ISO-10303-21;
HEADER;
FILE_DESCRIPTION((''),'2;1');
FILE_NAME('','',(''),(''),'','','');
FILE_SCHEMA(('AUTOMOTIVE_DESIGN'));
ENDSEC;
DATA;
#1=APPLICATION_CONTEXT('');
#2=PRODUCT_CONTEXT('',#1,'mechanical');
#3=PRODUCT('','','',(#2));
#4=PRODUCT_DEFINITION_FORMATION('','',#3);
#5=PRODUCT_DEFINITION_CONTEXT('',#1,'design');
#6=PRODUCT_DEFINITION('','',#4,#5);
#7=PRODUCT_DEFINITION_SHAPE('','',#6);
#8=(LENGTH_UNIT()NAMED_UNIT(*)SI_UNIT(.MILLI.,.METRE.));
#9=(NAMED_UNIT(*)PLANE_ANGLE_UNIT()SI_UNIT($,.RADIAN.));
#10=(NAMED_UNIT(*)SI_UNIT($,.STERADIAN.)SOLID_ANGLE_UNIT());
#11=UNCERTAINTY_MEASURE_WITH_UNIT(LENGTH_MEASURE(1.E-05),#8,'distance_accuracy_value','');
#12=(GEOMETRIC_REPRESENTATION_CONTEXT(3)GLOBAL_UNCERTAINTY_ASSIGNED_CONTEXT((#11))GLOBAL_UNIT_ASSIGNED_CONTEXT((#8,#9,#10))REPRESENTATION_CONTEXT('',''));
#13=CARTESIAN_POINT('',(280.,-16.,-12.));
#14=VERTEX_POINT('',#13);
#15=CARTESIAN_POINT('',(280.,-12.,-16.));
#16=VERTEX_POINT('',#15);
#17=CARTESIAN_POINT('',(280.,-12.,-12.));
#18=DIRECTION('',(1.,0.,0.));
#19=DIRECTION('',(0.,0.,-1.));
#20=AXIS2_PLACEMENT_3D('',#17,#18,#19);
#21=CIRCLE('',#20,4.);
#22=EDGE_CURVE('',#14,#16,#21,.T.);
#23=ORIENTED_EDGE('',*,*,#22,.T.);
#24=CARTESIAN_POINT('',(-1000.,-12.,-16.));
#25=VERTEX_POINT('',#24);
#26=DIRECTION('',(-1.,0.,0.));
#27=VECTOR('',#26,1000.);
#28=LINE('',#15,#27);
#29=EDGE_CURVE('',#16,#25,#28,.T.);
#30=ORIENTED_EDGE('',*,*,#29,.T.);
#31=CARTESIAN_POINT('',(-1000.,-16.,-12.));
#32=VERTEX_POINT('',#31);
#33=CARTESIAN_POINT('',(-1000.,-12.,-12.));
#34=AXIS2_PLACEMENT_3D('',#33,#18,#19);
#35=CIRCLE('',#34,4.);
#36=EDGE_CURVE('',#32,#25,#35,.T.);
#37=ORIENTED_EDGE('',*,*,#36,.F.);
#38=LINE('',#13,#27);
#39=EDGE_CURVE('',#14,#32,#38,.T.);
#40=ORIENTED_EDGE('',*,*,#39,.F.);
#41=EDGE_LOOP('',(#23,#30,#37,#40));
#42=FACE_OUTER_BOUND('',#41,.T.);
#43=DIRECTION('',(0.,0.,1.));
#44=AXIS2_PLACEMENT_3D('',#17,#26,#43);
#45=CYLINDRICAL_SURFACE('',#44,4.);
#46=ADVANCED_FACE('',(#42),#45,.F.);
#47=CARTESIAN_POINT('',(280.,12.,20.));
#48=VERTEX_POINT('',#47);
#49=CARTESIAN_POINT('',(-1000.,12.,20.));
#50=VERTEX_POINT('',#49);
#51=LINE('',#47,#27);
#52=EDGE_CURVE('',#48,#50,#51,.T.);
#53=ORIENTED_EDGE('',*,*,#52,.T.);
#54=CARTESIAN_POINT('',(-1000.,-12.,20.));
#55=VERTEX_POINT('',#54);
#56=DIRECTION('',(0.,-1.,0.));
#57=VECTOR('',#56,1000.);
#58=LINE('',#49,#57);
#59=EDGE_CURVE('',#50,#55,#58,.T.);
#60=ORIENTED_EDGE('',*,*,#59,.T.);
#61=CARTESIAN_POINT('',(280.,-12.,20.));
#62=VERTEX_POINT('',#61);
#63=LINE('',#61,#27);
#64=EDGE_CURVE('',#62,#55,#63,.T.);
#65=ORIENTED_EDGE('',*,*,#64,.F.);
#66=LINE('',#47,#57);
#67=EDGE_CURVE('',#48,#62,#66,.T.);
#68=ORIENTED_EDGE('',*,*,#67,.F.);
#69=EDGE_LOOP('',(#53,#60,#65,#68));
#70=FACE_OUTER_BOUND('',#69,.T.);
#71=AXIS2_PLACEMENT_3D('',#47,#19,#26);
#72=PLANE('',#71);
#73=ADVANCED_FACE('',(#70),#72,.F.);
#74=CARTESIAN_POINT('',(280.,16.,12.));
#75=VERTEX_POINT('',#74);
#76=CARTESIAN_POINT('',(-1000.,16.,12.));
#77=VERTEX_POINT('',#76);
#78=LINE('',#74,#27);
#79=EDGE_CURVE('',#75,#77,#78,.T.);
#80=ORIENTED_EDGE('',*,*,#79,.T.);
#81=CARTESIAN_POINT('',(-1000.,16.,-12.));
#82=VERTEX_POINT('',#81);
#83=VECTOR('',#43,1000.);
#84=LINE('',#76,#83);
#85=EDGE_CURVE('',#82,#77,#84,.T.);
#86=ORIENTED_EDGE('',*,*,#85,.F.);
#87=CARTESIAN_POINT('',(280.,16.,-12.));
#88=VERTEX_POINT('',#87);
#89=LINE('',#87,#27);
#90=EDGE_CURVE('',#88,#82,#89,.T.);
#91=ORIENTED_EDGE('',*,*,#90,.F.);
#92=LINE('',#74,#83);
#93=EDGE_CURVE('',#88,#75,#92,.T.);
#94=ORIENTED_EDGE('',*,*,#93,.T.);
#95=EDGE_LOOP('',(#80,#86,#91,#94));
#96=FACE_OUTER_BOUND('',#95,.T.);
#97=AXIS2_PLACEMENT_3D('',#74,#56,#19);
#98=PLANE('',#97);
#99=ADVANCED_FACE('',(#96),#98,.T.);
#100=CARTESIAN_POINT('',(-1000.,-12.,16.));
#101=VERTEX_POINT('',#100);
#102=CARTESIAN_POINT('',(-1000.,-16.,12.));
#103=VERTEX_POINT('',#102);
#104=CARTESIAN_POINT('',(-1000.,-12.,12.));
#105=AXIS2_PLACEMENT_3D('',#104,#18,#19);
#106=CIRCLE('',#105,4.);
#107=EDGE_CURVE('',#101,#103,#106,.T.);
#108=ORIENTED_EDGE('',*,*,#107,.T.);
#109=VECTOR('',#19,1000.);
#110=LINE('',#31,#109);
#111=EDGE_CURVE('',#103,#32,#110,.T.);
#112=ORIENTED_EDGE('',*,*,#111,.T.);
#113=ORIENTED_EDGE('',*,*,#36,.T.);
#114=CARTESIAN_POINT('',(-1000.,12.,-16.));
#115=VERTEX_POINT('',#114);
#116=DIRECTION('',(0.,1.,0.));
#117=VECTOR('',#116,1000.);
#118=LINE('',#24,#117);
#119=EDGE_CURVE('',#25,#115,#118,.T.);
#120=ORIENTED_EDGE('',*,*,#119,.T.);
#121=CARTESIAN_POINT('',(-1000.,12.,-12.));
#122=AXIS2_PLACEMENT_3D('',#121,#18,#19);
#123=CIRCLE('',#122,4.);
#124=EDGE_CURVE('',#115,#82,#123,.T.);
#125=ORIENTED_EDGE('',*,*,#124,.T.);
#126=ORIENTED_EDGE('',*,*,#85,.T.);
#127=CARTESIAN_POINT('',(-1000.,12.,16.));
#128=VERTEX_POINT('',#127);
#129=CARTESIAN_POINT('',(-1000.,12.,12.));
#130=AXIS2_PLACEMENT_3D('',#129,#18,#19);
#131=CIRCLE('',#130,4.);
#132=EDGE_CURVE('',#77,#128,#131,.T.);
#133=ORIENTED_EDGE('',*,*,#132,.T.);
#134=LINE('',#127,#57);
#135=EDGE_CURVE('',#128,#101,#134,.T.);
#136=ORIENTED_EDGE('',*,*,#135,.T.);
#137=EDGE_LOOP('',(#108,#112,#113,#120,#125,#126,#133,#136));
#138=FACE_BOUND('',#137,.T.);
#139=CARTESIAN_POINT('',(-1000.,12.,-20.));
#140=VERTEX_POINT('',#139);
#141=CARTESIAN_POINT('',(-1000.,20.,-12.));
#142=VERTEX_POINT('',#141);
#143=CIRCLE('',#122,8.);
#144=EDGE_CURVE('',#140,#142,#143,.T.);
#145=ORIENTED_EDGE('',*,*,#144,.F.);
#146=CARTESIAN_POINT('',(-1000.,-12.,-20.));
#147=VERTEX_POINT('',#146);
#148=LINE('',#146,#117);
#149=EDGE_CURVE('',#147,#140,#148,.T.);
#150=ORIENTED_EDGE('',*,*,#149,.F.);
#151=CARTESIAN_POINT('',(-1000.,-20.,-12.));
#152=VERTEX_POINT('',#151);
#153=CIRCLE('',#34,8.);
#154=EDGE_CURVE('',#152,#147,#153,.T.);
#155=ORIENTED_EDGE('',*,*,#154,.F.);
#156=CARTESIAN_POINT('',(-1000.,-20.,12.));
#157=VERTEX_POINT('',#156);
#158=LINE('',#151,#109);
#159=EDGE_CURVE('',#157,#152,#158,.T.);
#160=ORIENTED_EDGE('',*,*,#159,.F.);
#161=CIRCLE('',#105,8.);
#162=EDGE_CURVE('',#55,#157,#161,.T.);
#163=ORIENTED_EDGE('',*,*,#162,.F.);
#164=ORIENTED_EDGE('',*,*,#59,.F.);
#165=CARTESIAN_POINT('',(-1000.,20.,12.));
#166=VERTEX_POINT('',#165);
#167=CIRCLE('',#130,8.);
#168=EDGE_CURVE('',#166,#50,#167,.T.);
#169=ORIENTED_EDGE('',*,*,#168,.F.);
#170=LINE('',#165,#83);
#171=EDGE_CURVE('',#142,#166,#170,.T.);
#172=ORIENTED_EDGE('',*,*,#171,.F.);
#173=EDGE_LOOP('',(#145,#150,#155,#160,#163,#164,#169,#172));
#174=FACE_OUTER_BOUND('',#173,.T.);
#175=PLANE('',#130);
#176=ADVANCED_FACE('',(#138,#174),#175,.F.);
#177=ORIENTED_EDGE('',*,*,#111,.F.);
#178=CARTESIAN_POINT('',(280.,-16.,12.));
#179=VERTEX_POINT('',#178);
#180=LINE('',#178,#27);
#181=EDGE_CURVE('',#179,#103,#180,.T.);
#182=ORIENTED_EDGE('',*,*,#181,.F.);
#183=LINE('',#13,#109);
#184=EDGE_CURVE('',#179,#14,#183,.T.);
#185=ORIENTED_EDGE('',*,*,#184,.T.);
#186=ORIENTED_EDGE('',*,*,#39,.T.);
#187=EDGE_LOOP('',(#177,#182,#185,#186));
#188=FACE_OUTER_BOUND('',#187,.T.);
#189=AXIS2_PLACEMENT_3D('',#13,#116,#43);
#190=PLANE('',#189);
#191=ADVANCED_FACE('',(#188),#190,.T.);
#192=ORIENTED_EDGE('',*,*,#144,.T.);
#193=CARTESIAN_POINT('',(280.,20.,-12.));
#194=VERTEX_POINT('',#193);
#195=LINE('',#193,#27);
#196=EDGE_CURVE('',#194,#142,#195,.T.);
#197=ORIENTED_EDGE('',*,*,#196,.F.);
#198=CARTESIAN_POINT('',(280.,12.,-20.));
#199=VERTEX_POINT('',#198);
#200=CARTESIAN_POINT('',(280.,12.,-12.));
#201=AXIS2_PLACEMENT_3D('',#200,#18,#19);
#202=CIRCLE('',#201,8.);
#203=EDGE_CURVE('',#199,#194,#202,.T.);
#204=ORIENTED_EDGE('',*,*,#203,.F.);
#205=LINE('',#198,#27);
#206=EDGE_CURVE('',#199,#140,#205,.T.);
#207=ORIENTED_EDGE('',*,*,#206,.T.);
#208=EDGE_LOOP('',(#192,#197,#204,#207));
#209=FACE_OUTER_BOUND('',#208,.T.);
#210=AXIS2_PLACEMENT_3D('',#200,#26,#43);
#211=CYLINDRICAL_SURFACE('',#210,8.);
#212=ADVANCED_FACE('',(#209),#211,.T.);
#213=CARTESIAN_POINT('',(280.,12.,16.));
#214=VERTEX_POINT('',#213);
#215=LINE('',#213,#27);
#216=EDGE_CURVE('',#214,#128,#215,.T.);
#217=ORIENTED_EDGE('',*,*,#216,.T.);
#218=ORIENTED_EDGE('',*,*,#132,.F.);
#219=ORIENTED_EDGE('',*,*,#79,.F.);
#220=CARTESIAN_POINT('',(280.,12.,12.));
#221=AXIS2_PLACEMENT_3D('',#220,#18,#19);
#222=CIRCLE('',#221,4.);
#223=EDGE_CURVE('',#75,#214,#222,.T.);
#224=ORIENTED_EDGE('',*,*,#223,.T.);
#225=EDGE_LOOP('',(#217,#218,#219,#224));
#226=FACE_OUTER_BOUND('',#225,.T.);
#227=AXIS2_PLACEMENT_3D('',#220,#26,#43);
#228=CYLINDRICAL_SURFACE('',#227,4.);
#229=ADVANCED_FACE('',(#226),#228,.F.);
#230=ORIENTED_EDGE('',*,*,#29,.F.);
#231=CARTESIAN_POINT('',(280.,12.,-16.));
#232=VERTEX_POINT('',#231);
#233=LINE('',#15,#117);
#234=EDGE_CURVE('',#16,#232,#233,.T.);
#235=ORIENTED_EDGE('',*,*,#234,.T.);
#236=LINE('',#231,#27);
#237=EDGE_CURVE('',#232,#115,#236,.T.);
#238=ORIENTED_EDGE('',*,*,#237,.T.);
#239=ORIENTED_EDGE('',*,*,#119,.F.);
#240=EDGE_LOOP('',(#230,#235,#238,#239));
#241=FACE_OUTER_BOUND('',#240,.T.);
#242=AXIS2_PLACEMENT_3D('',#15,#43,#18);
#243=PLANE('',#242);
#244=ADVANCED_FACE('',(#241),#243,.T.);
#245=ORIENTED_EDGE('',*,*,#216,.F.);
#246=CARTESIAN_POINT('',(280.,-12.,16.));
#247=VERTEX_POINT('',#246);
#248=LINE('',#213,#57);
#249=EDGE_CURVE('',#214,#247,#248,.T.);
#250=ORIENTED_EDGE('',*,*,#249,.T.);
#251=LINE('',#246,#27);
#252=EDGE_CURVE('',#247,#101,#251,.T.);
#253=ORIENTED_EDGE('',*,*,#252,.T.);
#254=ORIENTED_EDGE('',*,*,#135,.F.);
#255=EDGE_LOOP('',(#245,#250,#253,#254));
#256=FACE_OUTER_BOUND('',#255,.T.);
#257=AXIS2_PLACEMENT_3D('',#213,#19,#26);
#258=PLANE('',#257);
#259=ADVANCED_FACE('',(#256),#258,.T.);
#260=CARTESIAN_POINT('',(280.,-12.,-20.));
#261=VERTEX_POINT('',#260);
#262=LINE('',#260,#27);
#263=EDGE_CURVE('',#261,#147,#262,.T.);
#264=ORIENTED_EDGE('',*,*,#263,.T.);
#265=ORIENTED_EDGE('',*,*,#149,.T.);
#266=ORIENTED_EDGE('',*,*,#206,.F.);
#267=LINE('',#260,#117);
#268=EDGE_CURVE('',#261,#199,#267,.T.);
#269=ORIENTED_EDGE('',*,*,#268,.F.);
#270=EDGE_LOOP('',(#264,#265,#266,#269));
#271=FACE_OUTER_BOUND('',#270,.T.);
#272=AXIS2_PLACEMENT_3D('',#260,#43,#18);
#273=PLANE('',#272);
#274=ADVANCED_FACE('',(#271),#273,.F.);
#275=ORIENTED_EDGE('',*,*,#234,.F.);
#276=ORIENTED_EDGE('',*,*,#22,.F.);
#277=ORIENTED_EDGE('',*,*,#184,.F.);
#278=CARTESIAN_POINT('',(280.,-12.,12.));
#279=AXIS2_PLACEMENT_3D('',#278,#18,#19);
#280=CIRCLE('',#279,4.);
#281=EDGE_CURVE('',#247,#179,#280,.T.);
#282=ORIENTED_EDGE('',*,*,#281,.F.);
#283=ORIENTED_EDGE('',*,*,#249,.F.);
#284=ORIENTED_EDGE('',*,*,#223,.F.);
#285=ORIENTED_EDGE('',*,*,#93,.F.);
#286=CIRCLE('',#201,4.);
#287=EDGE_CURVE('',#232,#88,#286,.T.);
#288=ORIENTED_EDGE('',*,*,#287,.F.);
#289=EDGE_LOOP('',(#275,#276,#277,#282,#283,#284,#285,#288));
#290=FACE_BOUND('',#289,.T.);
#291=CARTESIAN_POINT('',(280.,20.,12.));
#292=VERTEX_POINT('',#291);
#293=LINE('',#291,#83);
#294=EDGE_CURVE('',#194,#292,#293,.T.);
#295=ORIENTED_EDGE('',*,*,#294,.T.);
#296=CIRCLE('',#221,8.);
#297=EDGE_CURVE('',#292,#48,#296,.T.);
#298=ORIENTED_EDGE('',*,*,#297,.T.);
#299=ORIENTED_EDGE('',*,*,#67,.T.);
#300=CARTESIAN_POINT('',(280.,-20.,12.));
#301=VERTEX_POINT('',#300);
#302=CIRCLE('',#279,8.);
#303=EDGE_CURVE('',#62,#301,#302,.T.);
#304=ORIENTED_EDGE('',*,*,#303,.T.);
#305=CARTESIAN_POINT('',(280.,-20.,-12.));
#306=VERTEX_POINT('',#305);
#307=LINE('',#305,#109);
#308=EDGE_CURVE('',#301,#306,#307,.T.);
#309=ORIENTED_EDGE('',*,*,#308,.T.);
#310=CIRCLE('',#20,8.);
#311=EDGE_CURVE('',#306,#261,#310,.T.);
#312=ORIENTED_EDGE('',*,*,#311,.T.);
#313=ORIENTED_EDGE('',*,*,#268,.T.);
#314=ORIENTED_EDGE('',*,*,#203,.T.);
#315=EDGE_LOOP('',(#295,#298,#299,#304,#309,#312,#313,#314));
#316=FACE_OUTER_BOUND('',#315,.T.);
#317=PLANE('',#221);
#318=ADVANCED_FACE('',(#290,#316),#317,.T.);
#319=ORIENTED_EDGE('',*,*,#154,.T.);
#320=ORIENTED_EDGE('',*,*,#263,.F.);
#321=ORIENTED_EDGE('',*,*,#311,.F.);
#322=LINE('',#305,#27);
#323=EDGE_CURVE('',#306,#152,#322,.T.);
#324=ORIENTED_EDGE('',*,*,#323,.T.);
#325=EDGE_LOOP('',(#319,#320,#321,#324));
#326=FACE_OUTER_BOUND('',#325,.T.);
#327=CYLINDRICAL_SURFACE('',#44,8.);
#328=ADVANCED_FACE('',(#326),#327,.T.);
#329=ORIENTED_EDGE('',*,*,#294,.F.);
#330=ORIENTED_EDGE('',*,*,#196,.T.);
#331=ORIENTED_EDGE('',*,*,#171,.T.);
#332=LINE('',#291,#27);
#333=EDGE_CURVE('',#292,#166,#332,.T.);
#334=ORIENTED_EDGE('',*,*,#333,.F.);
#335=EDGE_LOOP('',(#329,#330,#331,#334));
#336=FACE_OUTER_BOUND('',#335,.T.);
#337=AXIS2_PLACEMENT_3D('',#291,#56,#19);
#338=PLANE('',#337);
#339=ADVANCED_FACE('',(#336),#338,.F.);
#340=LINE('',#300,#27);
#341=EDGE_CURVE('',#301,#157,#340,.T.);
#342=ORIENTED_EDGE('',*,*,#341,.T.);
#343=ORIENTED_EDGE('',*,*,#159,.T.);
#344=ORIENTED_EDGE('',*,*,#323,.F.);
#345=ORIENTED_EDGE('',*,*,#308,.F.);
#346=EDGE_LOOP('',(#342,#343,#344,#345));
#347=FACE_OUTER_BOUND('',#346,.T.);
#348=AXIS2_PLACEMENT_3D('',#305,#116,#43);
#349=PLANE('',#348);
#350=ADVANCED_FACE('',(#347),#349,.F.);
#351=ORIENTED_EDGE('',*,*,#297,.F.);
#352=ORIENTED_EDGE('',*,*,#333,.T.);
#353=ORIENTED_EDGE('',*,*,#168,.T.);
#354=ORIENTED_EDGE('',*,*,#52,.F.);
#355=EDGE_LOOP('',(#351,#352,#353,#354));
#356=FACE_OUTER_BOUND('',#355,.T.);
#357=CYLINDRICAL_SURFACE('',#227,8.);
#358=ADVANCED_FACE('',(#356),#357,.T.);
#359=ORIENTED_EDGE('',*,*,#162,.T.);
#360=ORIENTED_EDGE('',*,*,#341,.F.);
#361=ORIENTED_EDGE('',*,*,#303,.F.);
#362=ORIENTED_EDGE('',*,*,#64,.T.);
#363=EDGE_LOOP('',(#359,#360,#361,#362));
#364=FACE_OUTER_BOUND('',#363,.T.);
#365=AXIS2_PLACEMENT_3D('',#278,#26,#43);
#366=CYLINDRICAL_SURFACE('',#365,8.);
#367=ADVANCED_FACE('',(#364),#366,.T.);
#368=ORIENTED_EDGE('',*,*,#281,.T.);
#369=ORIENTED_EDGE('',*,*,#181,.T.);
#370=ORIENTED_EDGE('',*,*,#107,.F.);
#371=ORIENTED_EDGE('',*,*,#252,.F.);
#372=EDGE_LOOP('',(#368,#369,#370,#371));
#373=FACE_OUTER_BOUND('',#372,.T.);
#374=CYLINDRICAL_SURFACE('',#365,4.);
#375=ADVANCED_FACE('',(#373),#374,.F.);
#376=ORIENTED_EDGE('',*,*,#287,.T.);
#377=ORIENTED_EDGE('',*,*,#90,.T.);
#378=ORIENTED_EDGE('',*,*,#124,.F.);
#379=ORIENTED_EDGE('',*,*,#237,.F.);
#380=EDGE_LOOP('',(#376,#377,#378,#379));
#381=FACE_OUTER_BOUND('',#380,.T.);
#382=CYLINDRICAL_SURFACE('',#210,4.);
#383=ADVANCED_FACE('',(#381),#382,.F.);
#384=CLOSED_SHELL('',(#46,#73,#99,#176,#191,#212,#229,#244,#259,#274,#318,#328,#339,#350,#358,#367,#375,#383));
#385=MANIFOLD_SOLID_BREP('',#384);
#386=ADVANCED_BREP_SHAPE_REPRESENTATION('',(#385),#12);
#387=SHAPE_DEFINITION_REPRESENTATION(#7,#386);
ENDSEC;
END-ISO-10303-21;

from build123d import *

# Parameters (mm, degrees)
SQUARE_TUBE_40_X_40_X_4_1_DEPTH = 1280


with BuildPart() as part:
    # Sketch1 → Square Tube 40 X 40 X 4(1) (new body)
    with BuildSketch(Plane.YZ.offset(-1000)):
        with BuildLine():
            Line((-12, -20), (12, -20))
            ThreePointArc((12, -20), (17.656854249, -17.656854249), (20, -12))
            Line((20, -12), (20, 12))
            ThreePointArc((20, 12), (17.656854249, 17.656854249), (12, 20))
            Line((12, 20), (-12, 20))
            ThreePointArc((-12, 20), (-17.656854249, 17.656854249), (-20, 12))
            Line((-20, 12), (-20, -12))
            ThreePointArc((-20, -12), (-17.656854249, -17.656854249), (-12, -20))
        make_face()
        with BuildLine():
            Line((-12, -16), (12, -16))
            ThreePointArc((12, -16), (14.828427125, -14.828427125), (16, -12))
            Line((16, -12), (16, 12))
            ThreePointArc((16, 12), (14.828427125, 14.828427125), (12, 16))
            Line((12, 16), (-12, 16))
            ThreePointArc((-12, 16), (-14.828427125, 14.828427125), (-16, 12))
            Line((-16, 12), (-16, -12))
            ThreePointArc((-16, -12), (-14.828427125, -14.828427125), (-12, -16))
        make_face(mode=Mode.SUBTRACT)
    extrude(amount=SQUARE_TUBE_40_X_40_X_4_1_DEPTH)


solid = part.part
